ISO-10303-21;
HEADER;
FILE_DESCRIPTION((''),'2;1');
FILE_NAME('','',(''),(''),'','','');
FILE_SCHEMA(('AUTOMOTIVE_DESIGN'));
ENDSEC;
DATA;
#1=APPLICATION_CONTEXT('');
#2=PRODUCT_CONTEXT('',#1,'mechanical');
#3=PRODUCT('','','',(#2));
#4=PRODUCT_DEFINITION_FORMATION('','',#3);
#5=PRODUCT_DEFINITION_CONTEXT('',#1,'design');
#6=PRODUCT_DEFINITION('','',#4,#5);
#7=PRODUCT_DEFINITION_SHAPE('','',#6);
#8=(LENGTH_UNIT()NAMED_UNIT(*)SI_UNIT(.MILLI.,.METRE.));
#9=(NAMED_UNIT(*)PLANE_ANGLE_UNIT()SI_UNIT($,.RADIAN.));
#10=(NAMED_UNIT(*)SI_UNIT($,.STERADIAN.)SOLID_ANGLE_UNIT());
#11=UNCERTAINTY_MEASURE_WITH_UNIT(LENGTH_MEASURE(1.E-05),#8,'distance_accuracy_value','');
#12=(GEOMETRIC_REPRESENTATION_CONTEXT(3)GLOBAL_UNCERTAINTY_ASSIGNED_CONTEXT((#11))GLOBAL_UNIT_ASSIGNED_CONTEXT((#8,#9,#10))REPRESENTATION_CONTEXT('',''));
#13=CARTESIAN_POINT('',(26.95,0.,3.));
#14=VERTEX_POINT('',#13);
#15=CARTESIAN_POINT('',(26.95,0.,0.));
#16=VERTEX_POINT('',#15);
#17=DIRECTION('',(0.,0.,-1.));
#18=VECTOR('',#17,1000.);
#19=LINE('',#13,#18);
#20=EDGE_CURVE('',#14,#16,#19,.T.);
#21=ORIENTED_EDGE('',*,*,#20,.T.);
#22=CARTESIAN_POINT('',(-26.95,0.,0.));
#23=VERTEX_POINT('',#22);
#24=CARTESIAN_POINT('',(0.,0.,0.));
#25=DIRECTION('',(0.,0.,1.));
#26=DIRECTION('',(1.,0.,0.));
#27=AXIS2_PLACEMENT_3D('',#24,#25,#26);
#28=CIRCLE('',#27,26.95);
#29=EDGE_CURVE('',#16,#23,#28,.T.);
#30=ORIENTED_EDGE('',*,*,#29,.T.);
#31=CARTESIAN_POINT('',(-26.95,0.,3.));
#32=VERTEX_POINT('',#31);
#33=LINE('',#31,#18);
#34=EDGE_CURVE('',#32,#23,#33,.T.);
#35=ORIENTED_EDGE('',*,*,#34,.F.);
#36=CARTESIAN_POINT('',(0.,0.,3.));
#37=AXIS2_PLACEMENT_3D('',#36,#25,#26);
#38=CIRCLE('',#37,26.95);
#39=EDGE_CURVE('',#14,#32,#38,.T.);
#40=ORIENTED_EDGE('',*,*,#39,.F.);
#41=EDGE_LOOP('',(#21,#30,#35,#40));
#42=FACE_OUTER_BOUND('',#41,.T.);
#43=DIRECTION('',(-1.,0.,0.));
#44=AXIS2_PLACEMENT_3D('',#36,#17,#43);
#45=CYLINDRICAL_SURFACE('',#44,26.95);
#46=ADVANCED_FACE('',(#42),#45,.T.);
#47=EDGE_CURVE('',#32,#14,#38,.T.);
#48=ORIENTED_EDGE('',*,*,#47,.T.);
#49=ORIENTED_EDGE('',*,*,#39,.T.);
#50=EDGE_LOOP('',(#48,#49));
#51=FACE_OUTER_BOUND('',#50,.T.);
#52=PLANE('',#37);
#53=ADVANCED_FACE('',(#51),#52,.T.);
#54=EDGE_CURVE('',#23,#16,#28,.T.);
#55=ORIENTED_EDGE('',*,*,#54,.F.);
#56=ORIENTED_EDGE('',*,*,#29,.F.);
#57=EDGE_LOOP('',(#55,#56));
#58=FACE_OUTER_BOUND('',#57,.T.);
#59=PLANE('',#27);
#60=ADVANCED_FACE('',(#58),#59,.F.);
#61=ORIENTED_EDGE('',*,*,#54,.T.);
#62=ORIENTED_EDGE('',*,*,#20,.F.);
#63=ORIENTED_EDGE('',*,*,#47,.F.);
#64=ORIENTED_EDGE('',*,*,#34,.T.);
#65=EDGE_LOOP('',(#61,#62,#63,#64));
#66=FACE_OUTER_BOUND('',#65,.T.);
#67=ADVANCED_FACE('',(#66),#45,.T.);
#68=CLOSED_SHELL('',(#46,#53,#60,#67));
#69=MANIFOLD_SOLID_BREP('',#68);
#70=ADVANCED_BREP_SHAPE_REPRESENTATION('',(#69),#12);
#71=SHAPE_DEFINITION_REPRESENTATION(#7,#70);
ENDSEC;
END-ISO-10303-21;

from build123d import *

# Parameters (mm, degrees)
SKETCH_1_R      = 26.95
EXTRUDE_1_DEPTH = 3


with BuildPart() as part:
    # 草图1 → 凸台-拉伸1 (new body)
    with BuildSketch(Plane.XY):
        Circle(SKETCH_1_R)
    extrude(amount=EXTRUDE_1_DEPTH)


solid = part.part
